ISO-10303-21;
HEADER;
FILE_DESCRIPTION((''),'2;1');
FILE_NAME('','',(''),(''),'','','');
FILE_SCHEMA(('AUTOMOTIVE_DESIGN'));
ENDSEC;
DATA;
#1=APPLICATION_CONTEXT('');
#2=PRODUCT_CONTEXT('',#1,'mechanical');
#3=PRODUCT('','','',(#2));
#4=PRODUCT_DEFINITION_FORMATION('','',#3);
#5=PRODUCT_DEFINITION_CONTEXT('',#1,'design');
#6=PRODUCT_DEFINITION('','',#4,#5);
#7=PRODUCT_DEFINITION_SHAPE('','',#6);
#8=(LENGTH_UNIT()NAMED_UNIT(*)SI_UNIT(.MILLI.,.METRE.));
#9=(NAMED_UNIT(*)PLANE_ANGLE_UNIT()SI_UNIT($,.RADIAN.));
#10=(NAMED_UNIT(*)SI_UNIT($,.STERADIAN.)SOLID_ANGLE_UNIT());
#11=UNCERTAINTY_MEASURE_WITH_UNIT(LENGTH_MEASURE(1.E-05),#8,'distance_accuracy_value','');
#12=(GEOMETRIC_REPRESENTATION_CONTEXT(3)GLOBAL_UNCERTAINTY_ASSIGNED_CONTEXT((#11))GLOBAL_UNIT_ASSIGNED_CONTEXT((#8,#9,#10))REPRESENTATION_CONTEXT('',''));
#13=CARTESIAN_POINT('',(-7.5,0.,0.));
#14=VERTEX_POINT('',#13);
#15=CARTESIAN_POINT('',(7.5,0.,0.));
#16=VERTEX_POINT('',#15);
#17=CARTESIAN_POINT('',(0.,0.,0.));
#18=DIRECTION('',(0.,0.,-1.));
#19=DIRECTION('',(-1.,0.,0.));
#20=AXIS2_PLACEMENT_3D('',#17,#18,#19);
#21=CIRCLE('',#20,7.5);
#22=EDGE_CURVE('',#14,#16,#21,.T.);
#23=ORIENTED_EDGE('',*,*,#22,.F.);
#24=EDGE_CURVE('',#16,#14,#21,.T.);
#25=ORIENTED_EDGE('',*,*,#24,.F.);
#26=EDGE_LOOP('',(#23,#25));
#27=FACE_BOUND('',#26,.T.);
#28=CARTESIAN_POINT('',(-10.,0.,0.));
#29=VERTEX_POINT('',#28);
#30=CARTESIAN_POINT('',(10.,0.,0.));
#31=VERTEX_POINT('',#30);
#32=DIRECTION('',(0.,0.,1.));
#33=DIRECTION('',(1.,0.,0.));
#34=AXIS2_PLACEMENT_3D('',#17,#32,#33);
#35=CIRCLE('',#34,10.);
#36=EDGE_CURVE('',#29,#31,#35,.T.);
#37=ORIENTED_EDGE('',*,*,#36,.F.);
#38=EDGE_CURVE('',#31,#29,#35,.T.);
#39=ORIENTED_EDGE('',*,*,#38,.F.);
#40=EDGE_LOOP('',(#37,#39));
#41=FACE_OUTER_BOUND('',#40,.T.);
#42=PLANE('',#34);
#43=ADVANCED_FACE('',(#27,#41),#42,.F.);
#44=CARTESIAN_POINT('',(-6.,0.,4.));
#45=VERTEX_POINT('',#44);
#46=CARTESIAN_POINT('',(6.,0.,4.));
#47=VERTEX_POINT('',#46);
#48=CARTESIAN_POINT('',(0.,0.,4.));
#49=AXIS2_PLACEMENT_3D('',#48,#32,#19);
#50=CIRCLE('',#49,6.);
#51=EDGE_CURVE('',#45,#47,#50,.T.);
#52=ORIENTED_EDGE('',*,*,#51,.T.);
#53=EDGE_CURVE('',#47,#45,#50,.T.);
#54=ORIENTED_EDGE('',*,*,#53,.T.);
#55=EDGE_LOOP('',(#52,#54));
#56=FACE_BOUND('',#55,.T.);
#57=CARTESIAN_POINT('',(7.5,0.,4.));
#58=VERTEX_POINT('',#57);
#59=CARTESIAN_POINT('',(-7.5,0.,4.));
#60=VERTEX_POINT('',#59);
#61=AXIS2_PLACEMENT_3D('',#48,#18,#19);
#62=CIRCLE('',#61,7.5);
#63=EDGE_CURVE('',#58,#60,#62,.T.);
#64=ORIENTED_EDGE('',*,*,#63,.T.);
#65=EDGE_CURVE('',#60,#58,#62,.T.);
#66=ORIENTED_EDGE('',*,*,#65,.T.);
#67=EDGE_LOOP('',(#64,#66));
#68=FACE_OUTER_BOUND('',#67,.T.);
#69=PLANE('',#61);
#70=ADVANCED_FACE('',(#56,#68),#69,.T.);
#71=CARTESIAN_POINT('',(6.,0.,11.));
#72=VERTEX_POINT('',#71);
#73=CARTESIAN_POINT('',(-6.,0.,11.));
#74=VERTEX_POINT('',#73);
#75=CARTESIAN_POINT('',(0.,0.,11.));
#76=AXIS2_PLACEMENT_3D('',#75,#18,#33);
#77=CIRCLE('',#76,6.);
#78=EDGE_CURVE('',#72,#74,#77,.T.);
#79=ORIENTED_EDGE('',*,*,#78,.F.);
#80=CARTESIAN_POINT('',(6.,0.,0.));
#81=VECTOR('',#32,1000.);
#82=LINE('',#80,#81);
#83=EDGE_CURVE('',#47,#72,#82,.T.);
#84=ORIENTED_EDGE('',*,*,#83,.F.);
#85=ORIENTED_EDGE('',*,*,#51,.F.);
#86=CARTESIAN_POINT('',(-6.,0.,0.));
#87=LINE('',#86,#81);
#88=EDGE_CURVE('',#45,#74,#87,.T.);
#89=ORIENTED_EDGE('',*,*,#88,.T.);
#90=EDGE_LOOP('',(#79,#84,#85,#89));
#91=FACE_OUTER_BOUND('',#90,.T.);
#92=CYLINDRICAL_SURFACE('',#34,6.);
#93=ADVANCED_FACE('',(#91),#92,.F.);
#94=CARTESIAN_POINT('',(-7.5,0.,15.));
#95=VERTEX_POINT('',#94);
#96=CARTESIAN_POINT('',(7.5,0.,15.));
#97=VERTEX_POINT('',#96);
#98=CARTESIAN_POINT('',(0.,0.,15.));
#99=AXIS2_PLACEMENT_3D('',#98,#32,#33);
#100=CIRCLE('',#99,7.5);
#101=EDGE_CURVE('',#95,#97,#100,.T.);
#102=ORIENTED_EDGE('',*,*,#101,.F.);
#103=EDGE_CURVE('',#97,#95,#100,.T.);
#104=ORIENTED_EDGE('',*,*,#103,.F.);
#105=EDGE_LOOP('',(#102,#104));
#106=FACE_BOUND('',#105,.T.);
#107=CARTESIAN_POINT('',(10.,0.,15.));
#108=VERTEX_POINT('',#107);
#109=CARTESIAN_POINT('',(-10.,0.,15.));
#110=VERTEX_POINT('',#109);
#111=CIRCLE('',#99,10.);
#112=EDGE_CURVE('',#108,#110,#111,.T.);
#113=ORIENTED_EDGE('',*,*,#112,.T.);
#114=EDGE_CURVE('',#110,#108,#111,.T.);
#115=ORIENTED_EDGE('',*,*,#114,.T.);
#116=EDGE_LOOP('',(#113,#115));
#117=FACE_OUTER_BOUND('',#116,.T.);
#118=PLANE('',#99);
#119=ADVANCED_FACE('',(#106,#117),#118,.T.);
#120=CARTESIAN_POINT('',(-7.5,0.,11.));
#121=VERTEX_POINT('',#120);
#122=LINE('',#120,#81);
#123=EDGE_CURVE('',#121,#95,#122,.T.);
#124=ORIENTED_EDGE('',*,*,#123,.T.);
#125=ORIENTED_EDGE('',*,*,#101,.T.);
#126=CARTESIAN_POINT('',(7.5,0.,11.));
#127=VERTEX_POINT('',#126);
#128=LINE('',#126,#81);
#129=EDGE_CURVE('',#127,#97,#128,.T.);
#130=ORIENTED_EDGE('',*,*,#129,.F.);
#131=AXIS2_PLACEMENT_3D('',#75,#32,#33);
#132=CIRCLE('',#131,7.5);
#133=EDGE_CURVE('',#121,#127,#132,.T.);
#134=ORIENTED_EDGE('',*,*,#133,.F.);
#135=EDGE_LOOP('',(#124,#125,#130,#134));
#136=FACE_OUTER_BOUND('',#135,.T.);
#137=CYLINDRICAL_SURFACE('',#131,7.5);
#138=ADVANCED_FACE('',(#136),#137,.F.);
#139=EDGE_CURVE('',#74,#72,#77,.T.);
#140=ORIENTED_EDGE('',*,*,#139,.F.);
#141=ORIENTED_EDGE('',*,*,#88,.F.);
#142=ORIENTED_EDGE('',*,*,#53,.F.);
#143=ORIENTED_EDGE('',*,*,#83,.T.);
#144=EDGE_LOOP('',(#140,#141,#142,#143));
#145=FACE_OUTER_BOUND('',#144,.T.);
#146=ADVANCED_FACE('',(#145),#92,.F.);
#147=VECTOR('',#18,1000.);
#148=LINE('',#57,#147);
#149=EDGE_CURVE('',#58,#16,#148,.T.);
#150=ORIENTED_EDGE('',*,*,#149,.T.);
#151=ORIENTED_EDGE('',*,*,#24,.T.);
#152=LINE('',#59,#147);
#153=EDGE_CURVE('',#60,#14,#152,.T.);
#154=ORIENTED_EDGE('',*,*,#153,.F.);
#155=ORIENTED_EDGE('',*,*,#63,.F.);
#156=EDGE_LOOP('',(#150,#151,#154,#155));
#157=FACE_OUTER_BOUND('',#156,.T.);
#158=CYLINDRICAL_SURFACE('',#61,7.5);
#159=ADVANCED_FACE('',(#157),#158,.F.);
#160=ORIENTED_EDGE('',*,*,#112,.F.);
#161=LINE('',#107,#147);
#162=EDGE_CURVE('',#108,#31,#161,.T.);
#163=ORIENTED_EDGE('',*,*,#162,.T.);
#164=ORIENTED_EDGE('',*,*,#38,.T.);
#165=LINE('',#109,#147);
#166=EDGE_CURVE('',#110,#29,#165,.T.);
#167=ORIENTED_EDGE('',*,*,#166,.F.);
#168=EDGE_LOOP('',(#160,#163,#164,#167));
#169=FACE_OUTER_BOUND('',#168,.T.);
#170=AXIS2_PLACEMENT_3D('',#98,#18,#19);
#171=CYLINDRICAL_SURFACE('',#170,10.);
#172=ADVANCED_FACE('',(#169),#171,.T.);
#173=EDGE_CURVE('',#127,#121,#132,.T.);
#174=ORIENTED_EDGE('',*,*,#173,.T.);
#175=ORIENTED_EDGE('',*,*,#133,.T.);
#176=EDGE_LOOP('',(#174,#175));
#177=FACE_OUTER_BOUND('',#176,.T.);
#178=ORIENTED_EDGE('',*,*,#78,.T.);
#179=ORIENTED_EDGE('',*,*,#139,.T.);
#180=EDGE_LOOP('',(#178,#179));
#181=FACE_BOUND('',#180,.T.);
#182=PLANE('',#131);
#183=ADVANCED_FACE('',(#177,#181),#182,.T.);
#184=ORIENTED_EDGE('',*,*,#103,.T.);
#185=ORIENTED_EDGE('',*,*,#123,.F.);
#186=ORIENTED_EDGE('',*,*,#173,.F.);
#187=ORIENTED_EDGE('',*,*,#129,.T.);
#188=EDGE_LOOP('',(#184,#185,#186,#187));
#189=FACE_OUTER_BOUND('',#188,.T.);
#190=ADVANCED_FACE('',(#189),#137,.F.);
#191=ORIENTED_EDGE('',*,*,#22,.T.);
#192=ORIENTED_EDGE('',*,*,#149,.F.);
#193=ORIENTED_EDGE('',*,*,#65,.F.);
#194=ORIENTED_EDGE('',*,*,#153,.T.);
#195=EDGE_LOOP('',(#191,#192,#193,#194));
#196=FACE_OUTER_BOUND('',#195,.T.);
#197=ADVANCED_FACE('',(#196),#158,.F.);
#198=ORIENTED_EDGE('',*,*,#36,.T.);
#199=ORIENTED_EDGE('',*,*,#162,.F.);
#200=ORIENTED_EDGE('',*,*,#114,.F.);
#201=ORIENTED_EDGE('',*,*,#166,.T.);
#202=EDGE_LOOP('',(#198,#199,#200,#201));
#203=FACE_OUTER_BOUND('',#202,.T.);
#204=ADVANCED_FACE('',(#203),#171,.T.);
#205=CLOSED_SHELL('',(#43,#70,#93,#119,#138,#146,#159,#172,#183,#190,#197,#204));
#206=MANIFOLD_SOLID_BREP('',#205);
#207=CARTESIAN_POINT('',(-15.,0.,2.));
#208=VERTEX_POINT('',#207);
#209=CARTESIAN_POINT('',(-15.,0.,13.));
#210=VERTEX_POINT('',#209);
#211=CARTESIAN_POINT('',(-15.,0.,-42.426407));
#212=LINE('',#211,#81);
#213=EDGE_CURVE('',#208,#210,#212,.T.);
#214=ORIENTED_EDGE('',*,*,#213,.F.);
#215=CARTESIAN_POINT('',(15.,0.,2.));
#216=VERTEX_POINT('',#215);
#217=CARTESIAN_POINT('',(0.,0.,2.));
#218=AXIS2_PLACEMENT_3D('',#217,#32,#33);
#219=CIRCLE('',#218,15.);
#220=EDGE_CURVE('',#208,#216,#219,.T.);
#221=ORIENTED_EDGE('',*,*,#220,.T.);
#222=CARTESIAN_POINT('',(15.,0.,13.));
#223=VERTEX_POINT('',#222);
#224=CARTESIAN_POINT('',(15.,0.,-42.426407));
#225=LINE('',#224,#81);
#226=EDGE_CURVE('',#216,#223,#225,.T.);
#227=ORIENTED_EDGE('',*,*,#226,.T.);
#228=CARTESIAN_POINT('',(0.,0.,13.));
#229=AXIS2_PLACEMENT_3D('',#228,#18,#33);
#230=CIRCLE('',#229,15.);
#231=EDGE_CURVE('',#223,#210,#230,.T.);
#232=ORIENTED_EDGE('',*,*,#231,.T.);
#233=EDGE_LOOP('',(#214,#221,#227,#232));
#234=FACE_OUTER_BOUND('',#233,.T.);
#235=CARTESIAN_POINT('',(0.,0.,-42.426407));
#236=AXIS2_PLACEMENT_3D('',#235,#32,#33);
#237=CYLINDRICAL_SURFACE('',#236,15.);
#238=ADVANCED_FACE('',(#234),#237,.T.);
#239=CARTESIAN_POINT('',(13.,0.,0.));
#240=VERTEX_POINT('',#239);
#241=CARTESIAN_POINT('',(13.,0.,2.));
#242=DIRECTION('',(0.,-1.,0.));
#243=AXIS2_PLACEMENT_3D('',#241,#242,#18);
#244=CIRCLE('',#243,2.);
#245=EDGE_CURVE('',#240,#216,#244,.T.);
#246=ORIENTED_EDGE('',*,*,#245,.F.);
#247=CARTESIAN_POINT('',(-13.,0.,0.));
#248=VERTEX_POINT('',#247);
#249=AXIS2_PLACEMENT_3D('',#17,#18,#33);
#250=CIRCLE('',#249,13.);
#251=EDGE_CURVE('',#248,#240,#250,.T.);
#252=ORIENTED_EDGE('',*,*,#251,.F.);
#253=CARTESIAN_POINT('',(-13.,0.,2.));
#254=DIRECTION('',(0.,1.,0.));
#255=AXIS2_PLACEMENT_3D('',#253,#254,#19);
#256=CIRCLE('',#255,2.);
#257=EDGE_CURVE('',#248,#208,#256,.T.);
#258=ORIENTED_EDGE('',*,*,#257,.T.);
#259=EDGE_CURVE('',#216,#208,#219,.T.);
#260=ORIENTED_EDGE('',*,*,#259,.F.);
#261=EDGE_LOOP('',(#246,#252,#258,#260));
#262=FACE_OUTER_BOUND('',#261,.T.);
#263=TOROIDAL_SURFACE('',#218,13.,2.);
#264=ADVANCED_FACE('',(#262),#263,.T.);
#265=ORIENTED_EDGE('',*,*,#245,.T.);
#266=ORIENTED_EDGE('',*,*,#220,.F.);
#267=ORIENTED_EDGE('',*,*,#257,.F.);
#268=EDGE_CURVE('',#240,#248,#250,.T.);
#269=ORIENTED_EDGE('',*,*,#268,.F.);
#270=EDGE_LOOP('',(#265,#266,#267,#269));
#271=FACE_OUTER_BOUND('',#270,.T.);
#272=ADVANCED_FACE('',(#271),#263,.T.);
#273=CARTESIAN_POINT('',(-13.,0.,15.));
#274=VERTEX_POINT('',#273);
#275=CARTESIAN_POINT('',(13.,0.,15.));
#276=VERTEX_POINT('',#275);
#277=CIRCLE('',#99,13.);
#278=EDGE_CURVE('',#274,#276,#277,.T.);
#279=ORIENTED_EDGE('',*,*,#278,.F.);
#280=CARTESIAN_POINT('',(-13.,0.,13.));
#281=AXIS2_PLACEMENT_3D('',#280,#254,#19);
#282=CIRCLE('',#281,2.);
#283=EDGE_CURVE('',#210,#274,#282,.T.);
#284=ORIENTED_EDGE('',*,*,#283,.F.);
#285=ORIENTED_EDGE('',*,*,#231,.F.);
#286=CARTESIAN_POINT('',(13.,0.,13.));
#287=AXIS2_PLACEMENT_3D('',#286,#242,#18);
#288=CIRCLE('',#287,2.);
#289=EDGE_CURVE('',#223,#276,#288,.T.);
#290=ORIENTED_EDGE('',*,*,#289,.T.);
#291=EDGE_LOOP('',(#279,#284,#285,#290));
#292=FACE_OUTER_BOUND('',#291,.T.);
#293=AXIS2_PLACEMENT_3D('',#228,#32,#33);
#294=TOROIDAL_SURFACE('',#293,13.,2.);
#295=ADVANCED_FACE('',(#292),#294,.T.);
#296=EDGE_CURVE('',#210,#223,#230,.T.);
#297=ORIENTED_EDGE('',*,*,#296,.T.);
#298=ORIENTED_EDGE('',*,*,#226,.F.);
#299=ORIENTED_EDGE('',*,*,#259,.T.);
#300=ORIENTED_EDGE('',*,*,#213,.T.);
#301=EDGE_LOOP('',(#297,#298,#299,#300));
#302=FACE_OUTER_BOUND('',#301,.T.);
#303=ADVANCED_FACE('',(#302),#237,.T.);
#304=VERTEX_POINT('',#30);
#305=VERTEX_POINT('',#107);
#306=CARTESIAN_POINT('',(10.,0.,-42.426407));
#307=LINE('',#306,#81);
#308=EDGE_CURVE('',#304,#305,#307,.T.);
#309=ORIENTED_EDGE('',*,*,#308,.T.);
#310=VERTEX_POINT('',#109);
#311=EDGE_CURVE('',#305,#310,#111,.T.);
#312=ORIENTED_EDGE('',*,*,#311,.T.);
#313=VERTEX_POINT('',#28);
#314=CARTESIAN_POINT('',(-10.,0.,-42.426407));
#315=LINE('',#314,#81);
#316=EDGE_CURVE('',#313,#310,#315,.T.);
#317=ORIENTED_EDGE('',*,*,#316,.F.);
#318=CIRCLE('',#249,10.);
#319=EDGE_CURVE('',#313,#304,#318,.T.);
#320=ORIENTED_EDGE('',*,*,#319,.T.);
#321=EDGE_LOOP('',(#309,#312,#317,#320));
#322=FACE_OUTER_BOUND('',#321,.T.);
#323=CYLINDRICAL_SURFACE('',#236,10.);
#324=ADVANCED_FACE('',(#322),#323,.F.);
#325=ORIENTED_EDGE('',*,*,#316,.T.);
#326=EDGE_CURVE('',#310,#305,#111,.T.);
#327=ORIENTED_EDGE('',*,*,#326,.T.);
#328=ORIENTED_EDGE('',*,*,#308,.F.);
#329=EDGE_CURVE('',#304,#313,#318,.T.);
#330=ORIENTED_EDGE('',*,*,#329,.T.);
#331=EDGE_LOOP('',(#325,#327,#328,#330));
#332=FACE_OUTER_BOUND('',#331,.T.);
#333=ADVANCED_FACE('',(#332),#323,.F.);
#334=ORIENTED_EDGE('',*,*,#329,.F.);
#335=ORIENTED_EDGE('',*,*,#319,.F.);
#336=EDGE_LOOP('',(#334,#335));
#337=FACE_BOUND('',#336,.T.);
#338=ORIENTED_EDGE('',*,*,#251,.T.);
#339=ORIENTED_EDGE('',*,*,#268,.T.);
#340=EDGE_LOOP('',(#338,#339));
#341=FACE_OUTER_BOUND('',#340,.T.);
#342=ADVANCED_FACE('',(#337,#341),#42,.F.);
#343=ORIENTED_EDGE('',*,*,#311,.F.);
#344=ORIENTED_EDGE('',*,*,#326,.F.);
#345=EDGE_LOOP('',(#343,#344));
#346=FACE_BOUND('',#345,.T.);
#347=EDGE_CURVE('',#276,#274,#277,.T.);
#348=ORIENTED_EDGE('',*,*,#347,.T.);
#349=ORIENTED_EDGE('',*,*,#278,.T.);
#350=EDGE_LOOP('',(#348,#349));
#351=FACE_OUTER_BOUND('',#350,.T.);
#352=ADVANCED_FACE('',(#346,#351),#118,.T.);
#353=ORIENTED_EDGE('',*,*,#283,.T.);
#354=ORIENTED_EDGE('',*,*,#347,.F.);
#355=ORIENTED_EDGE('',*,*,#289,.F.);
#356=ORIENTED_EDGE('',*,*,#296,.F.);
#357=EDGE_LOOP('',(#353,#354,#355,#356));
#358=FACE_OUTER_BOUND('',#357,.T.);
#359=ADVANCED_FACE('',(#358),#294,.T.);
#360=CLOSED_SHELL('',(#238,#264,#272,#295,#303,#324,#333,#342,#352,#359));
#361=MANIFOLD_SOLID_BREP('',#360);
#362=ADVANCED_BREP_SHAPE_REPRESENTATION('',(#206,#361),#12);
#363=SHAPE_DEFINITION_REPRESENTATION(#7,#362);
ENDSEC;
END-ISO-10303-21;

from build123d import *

# Parameters (mm, degrees)
SKETCH1_R           = 10
BOSS_EXTRUDE1_DEPTH = 15
SKETCH2_R           = 15
SKETCH2_R_2         = 10
BOSS_EXTRUDE2_DEPTH = 15
SKETCH3_R           = 6
CUT_EXTRUDE1_DEPTH  = 26.980762114
SKETCH4_R           = 7.5
CUT_EXTRUDE2_DEPTH  = 4
CUT_EXTRUDE3_START  = -4
SKETCH5_R           = 7.5
CUT_EXTRUDE3_DEPTH  = 4
FILLET1_R           = 2


with BuildPart() as part:
    # Sketch1 → Boss-Extrude1 (new body)
    with BuildSketch(Plane.XY):
        Circle(SKETCH1_R)
    extrude(amount=BOSS_EXTRUDE1_DEPTH)

    # Sketch3 → Cut-Extrude1 (cut, through all)
    with BuildSketch(Plane.XY.offset(15)):
        Circle(SKETCH3_R)
    extrude(amount=-CUT_EXTRUDE1_DEPTH, mode=Mode.SUBTRACT)

    # Sketch4 → Cut-Extrude2 (cut)
    with BuildSketch(Plane.XY.offset(15)):
        Circle(SKETCH4_R)
    extrude(amount=-CUT_EXTRUDE2_DEPTH, mode=Mode.SUBTRACT)

    # Sketch5 → Cut-Extrude3 (cut)
    with BuildSketch(Plane(origin=(0, 0, 0), x_dir=(-1, 0, 0), z_dir=(0, 0, -1)).offset(CUT_EXTRUDE3_START)):
        with Locations(Location((0, 0, 0), (0, 0, 180))):
            Circle(SKETCH5_R)
    extrude(amount=CUT_EXTRUDE3_DEPTH, mode=Mode.SUBTRACT)


with BuildPart() as body_2:
    # Sketch2 → Boss-Extrude2 (new body)
    with BuildSketch(Plane.XY.offset(15)):
        Circle(SKETCH2_R)
        Circle(SKETCH2_R_2, mode=Mode.SUBTRACT)
    extrude(amount=-BOSS_EXTRUDE2_DEPTH)

    # Fillet1
    fillet1_edges = [body_2.edges().sort_by_distance(p)[0] for p in [
        (-15, 0, 15),
        (-15, 0, 0),
    ]]
    fillet(fillet1_edges, radius=FILLET1_R)


solid = Compound([part.part, body_2.part])
